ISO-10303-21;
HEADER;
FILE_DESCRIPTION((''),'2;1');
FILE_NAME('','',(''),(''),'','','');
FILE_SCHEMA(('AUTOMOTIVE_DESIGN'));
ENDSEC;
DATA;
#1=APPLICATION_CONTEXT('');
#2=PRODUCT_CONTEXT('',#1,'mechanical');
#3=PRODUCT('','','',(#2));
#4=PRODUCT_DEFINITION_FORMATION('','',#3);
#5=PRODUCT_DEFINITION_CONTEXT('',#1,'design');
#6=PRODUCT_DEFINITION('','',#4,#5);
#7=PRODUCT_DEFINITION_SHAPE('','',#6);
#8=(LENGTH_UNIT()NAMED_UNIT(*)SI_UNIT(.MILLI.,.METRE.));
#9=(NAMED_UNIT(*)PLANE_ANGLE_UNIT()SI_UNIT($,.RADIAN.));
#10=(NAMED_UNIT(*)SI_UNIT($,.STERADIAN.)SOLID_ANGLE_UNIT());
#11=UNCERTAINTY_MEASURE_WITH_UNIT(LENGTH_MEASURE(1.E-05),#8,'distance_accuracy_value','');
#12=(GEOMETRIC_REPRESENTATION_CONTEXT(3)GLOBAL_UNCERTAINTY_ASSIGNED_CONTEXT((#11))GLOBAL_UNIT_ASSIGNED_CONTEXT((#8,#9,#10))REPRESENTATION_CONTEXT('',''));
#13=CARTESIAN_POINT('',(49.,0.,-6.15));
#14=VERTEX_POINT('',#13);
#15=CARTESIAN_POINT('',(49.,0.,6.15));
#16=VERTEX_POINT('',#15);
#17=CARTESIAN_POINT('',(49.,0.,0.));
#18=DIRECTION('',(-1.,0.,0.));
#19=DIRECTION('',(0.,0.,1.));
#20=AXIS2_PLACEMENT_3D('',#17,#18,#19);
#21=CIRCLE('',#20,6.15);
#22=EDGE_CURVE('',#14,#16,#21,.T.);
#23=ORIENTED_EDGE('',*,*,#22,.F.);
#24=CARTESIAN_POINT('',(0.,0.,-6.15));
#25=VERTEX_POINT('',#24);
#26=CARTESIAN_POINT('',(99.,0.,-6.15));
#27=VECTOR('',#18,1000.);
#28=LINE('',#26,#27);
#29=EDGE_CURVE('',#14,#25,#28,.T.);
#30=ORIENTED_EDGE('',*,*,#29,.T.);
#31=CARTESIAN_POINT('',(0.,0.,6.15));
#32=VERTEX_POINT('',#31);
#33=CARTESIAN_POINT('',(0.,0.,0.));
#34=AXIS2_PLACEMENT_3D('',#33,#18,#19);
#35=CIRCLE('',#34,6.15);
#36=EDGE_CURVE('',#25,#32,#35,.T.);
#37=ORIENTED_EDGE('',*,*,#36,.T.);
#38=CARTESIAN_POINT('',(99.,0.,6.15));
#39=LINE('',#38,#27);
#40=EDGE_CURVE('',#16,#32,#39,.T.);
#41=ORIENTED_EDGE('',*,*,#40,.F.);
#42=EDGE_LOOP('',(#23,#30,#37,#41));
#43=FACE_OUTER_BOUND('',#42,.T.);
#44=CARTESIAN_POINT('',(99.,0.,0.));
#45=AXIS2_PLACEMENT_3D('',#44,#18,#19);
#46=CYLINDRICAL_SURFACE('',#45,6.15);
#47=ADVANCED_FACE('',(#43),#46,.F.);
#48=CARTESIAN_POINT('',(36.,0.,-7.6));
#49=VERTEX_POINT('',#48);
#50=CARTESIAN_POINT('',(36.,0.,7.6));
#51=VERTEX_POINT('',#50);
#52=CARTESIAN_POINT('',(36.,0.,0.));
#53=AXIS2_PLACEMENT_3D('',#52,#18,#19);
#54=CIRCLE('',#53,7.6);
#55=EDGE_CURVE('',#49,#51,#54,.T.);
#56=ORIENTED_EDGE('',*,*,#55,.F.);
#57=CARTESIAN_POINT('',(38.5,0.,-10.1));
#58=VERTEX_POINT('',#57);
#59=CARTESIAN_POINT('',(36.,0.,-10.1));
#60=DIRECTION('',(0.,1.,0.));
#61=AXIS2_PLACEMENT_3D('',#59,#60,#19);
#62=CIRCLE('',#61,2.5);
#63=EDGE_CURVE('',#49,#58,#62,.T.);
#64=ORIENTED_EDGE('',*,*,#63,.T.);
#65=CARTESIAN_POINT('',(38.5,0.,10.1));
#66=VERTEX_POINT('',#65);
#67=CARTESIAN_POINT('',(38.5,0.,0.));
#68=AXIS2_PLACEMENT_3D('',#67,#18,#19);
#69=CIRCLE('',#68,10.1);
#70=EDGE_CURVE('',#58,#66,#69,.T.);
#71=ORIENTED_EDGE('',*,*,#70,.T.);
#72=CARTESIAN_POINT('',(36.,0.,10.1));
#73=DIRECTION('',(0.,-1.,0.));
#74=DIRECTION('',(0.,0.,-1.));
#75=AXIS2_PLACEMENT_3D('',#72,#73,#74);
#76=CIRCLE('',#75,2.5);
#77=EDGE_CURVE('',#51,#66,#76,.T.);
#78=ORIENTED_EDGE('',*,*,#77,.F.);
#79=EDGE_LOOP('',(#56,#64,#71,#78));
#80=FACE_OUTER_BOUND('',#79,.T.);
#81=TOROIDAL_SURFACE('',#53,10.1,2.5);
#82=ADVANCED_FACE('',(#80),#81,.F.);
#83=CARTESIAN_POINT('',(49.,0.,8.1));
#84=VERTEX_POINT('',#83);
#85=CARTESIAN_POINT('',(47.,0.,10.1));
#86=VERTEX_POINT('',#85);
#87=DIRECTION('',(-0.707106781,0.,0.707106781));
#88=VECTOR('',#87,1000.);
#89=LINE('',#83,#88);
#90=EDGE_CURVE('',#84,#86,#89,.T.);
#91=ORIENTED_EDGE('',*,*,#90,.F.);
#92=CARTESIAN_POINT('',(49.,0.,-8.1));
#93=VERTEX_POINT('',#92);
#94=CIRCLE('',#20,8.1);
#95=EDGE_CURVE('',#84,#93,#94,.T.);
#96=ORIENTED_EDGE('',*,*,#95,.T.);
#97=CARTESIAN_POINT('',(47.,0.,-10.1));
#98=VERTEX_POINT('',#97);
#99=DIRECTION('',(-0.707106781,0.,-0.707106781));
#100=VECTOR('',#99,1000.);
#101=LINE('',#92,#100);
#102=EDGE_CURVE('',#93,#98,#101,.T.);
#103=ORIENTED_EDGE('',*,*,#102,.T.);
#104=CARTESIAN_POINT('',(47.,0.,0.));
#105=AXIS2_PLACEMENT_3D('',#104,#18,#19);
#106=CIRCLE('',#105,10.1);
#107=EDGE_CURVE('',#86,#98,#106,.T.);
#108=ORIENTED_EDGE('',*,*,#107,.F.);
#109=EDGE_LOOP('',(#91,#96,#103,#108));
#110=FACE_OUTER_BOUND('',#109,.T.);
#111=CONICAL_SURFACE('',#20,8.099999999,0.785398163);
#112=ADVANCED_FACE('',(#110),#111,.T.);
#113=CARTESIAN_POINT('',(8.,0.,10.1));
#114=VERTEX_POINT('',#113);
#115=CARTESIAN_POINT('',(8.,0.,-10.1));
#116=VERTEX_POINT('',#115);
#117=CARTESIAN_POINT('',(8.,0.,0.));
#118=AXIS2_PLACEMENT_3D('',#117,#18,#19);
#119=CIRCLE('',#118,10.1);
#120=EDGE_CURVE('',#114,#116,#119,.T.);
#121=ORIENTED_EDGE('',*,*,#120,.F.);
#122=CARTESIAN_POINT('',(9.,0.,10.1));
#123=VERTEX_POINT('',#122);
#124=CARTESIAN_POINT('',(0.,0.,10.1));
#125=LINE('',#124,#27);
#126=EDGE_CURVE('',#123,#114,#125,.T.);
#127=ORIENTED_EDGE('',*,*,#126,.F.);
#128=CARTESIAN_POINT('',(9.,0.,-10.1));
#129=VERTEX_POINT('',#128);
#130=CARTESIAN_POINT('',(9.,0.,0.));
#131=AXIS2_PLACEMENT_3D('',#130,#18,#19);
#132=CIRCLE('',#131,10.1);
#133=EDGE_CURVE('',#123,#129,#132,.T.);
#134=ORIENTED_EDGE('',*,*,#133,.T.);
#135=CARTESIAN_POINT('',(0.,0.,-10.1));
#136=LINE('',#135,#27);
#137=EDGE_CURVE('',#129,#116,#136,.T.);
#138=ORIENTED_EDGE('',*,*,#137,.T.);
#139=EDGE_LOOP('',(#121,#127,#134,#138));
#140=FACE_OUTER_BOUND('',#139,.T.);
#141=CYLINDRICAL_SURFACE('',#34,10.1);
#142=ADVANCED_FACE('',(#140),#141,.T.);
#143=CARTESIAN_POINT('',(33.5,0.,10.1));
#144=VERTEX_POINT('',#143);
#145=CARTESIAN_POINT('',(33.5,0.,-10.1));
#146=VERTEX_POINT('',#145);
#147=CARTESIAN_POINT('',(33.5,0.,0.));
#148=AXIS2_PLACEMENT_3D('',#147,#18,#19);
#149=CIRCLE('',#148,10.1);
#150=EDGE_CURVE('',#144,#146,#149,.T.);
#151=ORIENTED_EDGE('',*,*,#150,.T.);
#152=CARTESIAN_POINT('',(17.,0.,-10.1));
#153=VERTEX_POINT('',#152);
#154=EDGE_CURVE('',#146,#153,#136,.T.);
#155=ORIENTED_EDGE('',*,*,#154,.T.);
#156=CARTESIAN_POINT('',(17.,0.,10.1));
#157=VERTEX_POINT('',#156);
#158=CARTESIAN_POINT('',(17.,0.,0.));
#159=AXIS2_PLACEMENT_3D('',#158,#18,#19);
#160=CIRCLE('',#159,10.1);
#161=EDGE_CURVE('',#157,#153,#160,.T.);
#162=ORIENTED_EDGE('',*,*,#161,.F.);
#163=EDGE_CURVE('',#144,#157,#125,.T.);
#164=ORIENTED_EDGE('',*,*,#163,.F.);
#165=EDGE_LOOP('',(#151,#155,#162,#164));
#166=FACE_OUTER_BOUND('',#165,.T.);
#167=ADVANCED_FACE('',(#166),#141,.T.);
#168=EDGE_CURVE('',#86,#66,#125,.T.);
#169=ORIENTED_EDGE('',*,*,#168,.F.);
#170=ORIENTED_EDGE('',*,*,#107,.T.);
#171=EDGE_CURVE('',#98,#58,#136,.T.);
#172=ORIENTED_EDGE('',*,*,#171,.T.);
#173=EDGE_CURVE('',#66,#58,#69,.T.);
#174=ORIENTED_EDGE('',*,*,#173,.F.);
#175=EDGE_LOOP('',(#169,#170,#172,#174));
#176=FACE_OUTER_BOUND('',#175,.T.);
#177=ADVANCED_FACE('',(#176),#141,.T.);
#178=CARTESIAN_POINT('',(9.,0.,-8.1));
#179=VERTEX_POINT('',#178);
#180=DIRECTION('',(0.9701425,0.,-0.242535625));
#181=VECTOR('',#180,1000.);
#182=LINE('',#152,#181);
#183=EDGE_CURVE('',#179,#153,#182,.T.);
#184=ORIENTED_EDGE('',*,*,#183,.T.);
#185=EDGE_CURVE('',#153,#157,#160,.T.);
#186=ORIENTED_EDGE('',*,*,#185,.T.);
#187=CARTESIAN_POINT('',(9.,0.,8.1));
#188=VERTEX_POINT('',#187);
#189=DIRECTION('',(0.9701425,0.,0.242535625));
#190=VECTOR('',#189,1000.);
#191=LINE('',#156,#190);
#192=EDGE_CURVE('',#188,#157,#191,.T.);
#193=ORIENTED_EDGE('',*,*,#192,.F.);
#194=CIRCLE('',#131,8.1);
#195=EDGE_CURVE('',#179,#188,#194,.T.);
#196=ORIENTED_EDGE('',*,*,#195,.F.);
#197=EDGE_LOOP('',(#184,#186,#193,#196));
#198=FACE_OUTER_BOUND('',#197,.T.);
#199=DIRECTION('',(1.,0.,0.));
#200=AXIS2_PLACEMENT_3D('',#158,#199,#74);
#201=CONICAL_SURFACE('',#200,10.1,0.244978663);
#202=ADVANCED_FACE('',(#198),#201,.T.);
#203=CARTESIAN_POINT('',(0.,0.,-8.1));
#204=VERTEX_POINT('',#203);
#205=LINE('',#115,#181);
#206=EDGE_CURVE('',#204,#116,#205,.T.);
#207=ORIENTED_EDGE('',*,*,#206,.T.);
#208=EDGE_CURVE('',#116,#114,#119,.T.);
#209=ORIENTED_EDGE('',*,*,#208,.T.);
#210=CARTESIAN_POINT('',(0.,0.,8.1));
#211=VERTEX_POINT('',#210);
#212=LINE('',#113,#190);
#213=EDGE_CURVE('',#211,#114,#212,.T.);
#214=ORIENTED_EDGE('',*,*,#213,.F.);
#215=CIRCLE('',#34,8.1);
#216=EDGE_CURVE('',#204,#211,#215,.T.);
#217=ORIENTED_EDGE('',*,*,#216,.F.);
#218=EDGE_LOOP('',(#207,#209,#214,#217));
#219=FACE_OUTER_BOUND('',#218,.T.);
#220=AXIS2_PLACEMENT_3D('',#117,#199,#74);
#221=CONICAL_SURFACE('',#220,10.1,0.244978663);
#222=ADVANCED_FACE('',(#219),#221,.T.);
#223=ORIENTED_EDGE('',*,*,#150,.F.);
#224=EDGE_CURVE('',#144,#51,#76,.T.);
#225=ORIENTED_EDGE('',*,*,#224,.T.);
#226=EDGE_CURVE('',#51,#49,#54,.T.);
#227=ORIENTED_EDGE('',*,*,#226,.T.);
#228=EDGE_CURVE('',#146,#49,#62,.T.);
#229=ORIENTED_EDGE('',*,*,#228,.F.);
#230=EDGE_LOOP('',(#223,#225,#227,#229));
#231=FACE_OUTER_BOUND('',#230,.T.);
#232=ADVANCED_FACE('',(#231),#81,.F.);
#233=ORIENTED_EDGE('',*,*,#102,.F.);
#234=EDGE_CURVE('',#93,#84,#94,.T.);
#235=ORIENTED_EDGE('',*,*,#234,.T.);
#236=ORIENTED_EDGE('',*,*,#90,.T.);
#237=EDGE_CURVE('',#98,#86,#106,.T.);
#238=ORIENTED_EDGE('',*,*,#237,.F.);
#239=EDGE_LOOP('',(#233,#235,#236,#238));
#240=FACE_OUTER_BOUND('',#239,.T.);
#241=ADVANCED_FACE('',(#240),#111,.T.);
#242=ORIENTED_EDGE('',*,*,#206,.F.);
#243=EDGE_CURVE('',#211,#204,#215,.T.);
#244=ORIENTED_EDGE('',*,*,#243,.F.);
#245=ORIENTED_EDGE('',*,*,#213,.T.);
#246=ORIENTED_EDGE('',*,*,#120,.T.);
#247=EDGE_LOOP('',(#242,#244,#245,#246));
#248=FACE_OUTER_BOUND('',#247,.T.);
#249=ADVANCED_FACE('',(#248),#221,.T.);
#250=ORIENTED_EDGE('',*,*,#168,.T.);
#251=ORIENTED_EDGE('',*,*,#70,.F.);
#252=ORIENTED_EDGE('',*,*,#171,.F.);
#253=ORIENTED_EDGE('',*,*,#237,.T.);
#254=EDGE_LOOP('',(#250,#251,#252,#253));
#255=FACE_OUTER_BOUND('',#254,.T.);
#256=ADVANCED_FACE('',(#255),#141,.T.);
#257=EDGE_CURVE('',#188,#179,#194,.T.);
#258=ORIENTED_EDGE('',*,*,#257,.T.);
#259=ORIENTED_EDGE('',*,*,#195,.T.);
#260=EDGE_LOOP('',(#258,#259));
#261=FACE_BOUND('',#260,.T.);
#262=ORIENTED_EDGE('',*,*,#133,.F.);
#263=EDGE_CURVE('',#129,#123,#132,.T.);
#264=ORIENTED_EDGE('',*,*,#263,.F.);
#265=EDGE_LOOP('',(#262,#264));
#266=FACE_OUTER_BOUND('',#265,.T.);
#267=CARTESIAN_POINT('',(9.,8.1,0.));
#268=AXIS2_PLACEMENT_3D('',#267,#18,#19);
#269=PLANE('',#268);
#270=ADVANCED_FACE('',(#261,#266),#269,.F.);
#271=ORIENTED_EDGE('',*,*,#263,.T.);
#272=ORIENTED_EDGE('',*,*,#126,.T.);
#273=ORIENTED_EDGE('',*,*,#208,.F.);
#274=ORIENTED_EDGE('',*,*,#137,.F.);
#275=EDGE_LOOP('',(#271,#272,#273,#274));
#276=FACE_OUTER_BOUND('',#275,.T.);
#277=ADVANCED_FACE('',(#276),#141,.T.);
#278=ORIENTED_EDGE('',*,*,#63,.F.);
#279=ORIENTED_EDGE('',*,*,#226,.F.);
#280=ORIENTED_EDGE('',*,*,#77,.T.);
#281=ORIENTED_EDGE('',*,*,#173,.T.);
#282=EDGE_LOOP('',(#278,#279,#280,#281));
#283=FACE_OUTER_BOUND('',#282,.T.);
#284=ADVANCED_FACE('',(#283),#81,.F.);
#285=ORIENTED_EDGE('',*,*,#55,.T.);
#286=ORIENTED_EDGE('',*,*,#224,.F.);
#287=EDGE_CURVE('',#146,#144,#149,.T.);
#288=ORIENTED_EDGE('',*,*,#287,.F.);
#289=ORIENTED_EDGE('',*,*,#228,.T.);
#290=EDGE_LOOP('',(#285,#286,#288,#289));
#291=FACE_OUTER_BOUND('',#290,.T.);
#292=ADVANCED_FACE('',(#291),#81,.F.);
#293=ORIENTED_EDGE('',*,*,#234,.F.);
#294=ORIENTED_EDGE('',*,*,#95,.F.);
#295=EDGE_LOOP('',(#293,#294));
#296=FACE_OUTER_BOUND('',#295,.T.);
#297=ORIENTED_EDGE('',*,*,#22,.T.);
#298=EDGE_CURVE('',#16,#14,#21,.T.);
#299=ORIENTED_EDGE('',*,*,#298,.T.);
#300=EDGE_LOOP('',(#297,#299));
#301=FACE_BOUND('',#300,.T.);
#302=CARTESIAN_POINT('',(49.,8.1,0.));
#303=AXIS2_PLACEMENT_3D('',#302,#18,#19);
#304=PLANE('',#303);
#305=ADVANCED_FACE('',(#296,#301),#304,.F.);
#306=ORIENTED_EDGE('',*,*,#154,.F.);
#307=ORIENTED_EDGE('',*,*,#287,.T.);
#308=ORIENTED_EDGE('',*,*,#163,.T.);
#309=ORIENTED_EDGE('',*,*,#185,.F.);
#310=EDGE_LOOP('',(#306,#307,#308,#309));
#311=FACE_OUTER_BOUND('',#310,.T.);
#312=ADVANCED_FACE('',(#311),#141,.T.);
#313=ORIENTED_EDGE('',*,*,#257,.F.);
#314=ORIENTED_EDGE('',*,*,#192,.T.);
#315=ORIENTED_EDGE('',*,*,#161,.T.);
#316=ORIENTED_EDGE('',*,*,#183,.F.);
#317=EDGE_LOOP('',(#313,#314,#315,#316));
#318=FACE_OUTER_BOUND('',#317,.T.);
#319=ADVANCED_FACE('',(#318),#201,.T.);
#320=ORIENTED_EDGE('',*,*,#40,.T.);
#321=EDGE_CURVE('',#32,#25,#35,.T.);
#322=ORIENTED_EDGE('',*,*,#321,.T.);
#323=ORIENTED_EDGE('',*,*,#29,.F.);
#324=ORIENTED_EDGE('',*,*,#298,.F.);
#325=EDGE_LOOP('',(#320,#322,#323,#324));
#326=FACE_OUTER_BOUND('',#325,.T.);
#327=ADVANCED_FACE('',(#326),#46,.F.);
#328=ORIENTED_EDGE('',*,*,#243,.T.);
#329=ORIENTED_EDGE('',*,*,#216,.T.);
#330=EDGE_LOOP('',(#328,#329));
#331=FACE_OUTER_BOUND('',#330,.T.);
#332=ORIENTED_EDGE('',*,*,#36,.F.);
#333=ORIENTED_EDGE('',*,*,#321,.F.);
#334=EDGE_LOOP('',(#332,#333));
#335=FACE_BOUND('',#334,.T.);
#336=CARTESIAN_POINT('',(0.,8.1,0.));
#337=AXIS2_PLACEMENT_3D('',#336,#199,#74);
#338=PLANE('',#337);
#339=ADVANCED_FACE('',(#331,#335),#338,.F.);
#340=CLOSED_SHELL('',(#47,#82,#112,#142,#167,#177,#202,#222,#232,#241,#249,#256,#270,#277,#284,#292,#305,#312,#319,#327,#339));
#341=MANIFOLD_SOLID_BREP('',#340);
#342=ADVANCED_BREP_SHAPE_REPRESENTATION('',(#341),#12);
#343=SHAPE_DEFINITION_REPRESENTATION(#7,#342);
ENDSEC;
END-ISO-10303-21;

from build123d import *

# Parameters (mm, degrees)
SKETCH2_R          = 6.15
CUT_EXTRUDE1_DEPTH = 99


with BuildPart() as part:
    # Sketch1 → Revolve1 (revolve)
    with BuildSketch(Plane.XY, mode=Mode.PRIVATE) as revolve1_sk:
        with BuildLine():
            Line((17.000000001, 10.1), (9.000000001, 8.100000002))
            Line((9.000000001, 8.100000002), (9.000000001, 10.1))
            Line((9.000000001, 10.1), (8.000000001, 10.1))
            Line((8.000000001, 10.1), (0, 8.100000002))
            Line((0, 8.100000002), (0, 0))
            Line((0, 0), (49, 0))
            Line((49, 0), (49, 8.099999999))
            Line((49, 8.099999999), (46.999999999, 10.1))
            Line((46.999999999, 10.1), (38.500000001, 10.1))
            ThreePointArc((38.500000001, 10.1), (36.000000001, 7.6), (33.500000001, 10.1))
            Line((33.500000001, 10.1), (17.000000001, 10.1))
        make_face()
    revolve(revolve1_sk.sketch.rotate(Axis((0, 0, 0), (1, 0, 0)), 90), axis=Axis((0, 0, 0), (1, 0, 0)))

    # Sketch2 → Cut-Extrude1 (cut)
    with BuildSketch(Plane.ZY):
        Circle(SKETCH2_R)
    extrude(amount=-CUT_EXTRUDE1_DEPTH, mode=Mode.SUBTRACT)


solid = part.part
